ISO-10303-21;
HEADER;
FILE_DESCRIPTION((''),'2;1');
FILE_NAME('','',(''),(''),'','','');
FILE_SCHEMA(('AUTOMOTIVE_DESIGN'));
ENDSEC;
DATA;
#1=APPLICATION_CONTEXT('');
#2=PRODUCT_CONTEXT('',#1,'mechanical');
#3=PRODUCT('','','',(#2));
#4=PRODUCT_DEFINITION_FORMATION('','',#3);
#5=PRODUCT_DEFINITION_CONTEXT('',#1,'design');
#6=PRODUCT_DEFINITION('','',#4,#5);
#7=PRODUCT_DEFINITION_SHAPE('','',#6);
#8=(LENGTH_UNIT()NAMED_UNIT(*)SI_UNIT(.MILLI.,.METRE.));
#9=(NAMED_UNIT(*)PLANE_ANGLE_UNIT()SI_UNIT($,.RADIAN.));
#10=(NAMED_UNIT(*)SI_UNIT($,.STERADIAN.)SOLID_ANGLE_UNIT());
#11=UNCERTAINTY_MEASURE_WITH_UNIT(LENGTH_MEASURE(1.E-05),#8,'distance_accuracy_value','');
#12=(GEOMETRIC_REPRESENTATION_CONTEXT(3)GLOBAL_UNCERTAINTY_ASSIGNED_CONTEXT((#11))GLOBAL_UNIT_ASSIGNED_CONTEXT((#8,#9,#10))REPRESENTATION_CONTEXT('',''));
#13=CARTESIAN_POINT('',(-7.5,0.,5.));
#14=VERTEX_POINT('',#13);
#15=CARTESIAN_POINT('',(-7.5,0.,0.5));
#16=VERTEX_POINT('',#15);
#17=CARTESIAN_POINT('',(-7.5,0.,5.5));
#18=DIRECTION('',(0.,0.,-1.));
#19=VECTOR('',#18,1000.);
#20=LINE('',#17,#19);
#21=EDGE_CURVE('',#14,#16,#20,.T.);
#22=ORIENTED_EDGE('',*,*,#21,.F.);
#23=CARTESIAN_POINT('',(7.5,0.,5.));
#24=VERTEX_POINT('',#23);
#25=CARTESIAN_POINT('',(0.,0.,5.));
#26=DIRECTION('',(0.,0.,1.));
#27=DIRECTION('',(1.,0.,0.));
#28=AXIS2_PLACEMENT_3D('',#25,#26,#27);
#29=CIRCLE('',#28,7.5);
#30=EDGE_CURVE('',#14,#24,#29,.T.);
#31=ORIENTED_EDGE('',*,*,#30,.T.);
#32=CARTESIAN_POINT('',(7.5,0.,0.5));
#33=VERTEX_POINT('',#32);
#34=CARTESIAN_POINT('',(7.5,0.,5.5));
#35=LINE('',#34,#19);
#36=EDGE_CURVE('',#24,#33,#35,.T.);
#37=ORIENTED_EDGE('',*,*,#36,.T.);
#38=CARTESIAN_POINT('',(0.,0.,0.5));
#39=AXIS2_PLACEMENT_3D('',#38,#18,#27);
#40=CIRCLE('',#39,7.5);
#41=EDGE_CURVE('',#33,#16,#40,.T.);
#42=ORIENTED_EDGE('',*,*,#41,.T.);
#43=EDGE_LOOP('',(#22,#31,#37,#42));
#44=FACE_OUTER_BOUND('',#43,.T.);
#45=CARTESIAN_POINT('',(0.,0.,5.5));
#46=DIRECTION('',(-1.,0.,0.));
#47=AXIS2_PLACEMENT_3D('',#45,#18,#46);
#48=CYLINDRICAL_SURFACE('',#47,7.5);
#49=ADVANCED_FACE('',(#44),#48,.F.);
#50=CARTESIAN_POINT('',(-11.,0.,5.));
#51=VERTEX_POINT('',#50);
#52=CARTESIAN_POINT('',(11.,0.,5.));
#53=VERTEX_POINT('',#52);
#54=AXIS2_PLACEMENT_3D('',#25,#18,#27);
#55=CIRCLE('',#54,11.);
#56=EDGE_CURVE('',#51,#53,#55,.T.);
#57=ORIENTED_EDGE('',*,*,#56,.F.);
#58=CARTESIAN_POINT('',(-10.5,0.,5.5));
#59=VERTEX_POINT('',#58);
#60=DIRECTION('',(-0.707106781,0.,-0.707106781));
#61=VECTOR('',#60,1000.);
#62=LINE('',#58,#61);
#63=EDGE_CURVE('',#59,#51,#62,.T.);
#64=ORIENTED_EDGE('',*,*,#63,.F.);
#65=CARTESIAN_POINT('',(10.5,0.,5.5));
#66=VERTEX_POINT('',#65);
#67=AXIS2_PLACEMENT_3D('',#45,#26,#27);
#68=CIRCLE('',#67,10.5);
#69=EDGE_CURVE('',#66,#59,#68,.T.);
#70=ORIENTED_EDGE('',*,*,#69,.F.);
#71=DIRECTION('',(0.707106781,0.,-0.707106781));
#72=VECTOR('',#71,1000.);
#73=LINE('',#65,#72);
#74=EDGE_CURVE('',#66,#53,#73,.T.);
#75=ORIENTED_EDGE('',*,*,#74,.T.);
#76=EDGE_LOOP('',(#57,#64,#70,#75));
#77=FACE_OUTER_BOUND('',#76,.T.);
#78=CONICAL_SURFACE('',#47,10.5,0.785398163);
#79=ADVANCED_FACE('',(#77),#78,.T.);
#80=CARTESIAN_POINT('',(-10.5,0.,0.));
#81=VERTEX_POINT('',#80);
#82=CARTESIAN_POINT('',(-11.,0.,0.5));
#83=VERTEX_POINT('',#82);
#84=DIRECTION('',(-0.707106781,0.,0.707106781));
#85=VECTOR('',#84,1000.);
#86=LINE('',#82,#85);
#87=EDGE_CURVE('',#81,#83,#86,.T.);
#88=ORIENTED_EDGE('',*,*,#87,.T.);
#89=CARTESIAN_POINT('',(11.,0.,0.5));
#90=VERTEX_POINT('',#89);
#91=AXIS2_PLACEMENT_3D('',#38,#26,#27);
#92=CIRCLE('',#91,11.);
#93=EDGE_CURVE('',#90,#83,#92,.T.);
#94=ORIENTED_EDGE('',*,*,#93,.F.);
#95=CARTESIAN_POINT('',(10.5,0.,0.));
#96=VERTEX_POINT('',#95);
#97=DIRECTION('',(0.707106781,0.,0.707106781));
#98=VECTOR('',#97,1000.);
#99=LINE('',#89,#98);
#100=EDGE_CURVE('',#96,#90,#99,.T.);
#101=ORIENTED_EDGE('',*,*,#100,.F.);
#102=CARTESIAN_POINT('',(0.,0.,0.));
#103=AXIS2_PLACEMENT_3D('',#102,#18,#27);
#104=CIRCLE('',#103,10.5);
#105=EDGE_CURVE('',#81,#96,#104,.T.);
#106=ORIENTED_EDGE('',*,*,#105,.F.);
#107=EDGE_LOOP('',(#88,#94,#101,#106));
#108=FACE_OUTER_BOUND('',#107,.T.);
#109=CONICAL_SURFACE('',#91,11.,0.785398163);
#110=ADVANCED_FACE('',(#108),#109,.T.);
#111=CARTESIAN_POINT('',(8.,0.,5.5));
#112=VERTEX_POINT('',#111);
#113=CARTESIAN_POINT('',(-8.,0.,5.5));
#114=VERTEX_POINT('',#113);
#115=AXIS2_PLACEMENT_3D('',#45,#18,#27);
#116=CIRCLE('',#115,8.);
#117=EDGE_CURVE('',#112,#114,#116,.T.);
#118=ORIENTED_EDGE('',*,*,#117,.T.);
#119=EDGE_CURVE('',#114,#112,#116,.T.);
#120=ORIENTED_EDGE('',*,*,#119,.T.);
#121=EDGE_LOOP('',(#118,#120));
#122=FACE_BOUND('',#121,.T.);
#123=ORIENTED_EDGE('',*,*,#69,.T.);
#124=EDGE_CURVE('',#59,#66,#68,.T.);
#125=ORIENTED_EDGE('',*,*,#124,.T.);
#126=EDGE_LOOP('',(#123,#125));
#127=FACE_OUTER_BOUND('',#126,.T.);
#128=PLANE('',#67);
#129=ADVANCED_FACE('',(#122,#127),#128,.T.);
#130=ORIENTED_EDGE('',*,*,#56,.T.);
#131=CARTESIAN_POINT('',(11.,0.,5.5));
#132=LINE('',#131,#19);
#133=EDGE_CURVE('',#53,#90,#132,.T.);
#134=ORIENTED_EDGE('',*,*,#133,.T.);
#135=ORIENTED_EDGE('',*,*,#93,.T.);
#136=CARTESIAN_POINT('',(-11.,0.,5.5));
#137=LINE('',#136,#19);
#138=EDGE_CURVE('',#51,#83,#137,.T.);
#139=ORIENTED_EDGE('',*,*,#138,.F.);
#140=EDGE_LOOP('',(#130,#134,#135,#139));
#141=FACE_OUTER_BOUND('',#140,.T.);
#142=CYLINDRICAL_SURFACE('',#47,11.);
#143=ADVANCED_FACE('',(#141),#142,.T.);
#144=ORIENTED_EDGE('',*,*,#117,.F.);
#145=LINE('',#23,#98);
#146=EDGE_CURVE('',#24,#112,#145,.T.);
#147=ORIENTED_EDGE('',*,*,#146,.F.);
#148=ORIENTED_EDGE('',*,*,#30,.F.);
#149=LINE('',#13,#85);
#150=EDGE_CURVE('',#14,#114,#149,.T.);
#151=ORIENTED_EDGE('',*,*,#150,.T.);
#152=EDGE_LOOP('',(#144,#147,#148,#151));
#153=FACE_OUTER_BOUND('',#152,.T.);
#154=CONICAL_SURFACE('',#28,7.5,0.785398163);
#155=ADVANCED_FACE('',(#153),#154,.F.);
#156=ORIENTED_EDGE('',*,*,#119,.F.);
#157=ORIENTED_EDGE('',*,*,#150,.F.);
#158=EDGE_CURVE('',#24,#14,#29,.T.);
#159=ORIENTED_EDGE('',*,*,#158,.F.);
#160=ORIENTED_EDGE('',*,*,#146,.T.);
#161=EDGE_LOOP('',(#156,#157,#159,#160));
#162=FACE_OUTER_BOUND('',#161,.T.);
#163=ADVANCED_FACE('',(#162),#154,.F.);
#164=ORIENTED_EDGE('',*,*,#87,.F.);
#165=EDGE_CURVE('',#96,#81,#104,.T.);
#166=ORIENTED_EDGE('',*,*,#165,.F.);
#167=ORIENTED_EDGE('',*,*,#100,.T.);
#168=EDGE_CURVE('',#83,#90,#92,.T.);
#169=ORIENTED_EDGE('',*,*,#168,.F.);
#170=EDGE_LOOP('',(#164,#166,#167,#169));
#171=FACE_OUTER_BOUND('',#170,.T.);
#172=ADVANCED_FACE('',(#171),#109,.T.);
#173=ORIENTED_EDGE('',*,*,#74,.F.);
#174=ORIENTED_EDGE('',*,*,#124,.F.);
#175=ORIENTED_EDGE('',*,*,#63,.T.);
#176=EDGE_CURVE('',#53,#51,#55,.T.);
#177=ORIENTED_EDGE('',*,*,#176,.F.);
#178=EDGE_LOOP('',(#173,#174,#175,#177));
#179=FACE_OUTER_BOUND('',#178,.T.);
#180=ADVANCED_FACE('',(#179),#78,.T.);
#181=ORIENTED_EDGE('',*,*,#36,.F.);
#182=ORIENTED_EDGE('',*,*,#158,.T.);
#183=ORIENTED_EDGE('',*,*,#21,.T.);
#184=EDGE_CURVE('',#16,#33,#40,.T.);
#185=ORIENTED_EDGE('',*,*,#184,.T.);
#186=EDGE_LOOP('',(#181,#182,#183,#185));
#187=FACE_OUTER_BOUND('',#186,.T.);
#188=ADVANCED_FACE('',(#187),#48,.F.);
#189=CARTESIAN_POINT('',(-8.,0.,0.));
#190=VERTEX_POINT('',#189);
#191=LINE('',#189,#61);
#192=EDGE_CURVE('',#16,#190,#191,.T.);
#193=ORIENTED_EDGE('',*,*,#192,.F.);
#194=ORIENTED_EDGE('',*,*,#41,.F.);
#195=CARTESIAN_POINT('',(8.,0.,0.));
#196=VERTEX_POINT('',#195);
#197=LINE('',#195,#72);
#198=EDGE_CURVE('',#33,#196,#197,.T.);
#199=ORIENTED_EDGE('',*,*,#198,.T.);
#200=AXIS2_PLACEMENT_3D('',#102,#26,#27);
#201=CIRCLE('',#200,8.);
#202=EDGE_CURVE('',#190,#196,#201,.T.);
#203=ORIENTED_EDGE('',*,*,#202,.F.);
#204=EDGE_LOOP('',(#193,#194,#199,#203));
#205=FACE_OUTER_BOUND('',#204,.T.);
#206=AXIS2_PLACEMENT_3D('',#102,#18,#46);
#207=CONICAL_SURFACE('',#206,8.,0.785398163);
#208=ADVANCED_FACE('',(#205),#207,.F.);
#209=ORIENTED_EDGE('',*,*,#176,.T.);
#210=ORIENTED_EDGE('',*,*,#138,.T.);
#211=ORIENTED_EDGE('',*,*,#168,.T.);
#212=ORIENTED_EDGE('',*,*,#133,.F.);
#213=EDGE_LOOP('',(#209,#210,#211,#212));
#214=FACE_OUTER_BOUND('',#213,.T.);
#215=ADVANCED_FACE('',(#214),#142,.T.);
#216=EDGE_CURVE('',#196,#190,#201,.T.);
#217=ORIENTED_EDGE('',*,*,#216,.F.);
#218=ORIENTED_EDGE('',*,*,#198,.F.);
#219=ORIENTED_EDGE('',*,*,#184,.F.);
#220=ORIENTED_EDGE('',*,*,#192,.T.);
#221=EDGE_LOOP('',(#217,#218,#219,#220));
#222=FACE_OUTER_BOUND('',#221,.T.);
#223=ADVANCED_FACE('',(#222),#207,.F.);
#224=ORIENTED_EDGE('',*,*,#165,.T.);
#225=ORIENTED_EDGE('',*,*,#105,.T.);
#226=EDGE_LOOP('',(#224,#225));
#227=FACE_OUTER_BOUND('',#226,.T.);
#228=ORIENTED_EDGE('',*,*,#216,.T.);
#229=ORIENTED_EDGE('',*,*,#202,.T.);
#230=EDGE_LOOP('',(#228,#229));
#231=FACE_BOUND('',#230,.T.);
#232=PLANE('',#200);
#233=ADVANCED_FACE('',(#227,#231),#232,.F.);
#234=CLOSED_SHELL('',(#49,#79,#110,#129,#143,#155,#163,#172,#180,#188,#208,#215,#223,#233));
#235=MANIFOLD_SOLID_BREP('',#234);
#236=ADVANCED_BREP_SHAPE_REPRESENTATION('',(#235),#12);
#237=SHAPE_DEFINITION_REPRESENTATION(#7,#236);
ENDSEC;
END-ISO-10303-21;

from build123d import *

# Parameters (mm, degrees)
SKETCH1_R           = 11
SKETCH1_R_2         = 7.5
BOSS_EXTRUDE1_DEPTH = 5.5
CHAMFER1_SIZE       = 0.5


with BuildPart() as part:
    # Sketch1 → Boss-Extrude1 (new body)
    with BuildSketch(Plane.XY):
        Circle(SKETCH1_R)
        Circle(SKETCH1_R_2, mode=Mode.SUBTRACT)
    extrude(amount=BOSS_EXTRUDE1_DEPTH)

    # Chamfer1
    chamfer1_edges = [part.edges().sort_by_distance(p)[0] for p in [
        (-11, 0, 0),
        (-11, 0, 5.5),
        (-7.5, 0, 0),
        (-7.5, 0, 5.5),
    ]]
    chamfer(chamfer1_edges, length=CHAMFER1_SIZE)


solid = part.part
